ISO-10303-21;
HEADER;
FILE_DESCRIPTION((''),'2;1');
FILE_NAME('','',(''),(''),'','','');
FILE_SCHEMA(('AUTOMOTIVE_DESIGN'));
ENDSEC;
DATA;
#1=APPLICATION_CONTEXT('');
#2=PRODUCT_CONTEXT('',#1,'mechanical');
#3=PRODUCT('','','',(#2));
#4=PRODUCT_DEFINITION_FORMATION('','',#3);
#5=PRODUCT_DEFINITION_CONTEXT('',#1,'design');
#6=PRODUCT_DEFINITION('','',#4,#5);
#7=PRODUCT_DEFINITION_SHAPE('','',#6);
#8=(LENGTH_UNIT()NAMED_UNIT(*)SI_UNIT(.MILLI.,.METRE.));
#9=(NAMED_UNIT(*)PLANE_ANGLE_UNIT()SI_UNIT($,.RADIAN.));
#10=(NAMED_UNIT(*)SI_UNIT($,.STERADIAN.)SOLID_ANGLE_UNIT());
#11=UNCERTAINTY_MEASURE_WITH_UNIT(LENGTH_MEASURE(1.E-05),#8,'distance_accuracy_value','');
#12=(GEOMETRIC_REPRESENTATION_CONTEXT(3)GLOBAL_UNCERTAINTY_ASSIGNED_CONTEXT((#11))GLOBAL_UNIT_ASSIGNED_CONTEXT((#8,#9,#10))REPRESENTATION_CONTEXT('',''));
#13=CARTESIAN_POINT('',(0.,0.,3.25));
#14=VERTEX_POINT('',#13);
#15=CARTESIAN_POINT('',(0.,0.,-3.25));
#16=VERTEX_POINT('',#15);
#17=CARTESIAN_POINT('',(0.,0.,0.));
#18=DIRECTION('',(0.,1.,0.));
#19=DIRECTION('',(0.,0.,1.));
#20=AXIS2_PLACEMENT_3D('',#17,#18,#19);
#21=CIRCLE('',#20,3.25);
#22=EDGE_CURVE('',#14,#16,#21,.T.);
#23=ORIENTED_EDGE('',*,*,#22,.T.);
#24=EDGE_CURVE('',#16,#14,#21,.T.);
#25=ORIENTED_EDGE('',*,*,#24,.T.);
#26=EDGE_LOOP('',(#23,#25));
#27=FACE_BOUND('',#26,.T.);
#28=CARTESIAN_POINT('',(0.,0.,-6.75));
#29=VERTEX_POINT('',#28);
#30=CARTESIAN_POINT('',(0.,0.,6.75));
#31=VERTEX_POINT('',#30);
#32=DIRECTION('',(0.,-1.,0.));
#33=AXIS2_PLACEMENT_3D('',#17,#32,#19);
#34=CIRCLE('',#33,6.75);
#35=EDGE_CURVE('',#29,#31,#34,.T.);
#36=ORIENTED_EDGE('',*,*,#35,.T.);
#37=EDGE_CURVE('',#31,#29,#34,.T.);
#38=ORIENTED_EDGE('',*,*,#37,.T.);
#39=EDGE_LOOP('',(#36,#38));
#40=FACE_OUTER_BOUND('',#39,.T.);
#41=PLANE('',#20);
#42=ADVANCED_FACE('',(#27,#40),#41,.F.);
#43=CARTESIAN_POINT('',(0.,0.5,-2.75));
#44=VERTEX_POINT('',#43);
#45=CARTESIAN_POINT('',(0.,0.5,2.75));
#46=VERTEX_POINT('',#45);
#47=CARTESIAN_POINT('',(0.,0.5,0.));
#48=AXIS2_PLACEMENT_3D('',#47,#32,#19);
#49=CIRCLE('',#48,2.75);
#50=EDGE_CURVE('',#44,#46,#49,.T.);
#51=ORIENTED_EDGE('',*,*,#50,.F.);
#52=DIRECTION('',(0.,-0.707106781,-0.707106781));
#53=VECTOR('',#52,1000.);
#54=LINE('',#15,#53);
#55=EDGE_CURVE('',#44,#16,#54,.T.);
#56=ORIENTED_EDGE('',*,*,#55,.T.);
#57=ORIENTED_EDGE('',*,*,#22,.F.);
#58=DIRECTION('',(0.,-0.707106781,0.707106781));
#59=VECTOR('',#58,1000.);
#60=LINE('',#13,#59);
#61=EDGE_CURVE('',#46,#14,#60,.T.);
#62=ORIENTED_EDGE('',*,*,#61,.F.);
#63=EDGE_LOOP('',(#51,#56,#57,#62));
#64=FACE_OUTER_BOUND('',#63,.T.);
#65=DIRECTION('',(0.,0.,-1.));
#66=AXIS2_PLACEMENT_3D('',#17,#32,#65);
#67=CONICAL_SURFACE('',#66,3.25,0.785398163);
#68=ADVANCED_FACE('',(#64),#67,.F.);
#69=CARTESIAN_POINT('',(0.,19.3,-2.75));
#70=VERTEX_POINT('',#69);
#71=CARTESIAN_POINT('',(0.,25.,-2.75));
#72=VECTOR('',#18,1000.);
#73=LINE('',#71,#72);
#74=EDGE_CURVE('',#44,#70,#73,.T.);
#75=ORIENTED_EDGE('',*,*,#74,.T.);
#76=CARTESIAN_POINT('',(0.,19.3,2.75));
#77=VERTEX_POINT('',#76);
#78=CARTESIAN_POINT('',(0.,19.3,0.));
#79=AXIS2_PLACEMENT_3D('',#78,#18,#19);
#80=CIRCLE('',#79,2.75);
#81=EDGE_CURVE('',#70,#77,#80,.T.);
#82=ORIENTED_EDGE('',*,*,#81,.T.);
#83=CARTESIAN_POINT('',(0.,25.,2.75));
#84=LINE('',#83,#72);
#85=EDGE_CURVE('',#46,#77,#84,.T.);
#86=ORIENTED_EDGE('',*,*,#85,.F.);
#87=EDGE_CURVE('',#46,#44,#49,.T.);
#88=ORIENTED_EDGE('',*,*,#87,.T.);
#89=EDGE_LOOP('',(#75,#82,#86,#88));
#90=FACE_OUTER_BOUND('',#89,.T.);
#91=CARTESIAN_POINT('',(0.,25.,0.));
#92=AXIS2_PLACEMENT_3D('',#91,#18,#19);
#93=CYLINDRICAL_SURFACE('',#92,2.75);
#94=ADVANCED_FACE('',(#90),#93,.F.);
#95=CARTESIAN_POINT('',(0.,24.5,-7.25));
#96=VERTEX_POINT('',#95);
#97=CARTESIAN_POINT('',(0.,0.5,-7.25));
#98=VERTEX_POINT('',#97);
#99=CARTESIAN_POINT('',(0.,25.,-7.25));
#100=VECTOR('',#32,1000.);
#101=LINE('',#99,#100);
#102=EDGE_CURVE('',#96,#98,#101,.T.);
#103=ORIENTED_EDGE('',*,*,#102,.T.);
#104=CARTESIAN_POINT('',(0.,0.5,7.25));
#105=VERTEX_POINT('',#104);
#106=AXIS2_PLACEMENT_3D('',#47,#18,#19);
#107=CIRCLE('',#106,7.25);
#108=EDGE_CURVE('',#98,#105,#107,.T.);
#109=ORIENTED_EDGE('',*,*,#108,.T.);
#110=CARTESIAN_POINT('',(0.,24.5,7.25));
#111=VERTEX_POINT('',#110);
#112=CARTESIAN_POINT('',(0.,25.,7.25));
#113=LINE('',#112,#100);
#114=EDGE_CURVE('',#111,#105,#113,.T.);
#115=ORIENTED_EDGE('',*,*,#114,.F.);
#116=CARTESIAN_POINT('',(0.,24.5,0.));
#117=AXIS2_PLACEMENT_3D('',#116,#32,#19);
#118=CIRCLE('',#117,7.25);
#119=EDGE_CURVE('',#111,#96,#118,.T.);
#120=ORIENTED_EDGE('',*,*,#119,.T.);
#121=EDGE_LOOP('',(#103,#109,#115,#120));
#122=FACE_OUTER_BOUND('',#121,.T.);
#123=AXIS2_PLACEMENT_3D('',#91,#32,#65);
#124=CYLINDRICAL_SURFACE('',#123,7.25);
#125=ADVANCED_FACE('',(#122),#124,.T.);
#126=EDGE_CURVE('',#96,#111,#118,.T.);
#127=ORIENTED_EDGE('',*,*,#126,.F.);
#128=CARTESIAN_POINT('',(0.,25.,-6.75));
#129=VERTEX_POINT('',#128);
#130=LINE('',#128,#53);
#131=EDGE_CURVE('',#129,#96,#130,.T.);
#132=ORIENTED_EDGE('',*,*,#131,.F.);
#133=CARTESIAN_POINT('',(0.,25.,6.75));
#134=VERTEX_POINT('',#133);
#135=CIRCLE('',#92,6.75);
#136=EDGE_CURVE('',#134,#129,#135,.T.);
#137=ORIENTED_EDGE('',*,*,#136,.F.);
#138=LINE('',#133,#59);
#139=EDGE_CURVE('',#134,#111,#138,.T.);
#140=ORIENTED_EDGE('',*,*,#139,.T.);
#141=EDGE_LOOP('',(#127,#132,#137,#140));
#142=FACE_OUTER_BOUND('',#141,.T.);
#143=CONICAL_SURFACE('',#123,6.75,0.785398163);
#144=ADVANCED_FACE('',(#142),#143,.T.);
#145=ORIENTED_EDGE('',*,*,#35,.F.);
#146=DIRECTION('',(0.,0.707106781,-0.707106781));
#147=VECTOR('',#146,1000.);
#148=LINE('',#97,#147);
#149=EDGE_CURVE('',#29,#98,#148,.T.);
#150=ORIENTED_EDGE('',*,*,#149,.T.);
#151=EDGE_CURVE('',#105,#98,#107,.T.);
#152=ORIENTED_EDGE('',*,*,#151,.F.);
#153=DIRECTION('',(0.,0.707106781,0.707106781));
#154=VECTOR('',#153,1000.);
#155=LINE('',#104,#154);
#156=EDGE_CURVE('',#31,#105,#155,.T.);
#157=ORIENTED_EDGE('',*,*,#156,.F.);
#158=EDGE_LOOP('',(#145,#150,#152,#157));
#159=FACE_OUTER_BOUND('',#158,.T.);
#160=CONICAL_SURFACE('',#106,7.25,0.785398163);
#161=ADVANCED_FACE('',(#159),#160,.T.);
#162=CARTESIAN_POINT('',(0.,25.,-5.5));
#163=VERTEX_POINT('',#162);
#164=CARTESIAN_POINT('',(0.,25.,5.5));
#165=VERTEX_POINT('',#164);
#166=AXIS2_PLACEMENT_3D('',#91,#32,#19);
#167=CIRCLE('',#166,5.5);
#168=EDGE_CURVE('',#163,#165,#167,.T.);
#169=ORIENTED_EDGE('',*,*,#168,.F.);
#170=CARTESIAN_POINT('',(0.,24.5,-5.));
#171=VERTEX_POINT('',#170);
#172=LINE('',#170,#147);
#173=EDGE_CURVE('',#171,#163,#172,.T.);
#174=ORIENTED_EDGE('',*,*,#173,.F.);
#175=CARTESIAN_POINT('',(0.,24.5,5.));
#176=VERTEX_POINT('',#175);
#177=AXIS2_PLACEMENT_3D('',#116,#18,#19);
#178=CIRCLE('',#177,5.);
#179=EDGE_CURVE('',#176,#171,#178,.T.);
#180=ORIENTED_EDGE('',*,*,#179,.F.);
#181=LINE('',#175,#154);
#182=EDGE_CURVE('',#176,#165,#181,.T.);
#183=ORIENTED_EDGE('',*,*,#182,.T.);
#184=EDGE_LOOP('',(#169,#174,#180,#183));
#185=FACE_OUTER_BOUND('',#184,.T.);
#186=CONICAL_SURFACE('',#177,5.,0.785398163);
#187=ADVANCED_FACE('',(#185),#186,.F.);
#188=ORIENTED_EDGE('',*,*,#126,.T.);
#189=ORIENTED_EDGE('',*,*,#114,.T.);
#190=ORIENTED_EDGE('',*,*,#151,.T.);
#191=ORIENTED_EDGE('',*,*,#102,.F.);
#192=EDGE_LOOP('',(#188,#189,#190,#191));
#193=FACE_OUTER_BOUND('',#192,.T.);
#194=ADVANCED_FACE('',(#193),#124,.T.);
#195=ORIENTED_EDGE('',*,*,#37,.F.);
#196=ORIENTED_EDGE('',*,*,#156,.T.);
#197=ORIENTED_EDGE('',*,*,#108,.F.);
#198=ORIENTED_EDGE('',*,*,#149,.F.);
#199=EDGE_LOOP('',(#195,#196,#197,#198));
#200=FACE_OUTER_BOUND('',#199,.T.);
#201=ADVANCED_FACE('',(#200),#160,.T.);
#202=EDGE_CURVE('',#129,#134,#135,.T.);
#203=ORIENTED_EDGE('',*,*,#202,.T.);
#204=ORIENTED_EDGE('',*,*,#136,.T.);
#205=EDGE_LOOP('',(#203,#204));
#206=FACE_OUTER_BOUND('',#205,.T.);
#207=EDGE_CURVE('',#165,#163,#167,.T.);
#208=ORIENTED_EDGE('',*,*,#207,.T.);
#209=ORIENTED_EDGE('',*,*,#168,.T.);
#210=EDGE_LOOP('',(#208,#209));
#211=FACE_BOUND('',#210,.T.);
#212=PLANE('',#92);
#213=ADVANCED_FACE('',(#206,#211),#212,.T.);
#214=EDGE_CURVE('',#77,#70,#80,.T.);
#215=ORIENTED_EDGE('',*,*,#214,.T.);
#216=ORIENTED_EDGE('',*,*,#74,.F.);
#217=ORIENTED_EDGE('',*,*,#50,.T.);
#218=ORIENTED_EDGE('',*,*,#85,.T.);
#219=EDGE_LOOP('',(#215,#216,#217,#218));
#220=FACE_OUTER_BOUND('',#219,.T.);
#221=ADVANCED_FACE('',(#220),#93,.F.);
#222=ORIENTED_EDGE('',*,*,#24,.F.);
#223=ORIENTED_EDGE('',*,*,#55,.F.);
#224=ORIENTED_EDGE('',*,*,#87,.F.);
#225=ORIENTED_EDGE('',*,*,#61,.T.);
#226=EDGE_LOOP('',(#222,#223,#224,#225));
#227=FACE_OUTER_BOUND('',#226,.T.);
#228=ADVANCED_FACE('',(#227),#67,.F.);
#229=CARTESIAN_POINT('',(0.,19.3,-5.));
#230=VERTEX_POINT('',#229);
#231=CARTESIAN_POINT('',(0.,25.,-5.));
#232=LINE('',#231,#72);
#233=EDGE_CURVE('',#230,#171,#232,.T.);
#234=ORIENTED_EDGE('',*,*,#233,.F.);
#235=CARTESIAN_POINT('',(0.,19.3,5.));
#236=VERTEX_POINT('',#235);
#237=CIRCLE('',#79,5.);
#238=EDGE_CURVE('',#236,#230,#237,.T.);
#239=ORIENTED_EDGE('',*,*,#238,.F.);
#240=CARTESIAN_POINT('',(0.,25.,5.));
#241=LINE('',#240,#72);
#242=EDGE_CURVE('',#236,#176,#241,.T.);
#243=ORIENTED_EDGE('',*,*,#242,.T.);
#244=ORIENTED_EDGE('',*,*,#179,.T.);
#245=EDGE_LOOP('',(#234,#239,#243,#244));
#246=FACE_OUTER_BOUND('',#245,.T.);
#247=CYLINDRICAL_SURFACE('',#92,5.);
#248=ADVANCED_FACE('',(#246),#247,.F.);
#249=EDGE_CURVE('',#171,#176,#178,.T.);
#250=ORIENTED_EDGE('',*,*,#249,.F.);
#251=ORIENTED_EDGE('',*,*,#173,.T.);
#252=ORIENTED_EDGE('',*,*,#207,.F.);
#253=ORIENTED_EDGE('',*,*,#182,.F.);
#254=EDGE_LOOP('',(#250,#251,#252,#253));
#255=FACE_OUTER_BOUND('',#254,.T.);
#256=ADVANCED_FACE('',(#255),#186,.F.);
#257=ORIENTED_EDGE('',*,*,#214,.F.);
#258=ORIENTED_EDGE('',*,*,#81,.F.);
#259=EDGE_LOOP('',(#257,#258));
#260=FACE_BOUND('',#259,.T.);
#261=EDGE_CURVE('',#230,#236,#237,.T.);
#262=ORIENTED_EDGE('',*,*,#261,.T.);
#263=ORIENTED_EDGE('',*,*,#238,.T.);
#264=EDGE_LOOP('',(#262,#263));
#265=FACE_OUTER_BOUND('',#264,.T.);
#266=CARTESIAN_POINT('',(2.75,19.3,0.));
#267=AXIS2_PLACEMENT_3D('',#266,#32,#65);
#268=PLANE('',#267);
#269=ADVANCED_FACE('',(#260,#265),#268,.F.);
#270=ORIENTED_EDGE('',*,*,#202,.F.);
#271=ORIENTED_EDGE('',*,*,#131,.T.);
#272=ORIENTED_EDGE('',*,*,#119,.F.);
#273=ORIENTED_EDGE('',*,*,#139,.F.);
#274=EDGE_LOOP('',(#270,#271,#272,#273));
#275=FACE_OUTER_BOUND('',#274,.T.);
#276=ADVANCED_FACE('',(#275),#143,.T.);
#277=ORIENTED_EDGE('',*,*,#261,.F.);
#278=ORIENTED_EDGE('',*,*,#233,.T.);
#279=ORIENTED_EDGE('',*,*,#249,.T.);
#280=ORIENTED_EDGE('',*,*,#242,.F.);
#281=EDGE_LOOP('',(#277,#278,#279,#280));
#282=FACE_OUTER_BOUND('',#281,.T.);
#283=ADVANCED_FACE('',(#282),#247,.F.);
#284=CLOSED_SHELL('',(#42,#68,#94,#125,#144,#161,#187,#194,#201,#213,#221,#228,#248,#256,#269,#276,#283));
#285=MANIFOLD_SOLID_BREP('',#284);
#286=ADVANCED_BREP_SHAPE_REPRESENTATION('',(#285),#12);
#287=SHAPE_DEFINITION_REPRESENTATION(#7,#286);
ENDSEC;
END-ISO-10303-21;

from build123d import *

# Parameters (mm, degrees)
SKETCH1_R                                       = 7.25
BOSS_EXTRUDE1_DEPTH                             = 25
HOLE_SIZE_BY_HEX_SOCKET_SCREW_TYPE1_D           = 5.5
HOLE_SIZE_BY_HEX_SOCKET_SCREW_TYPE1_CBORE_D     = 10
HOLE_SIZE_BY_HEX_SOCKET_SCREW_TYPE1_CBORE_DEPTH = 5.7
CHAMFER1_SIZE                                   = 0.5


with BuildPart() as part:
    # Sketch1 → Boss-Extrude1 (new body)
    with BuildSketch(Plane(origin=(0, 0, 0), x_dir=(1, 0, 0), z_dir=(0, 1, 0))):
        with Locations(Location((0, 0, 0), (0, 0, 270))):
            Circle(SKETCH1_R)
    extrude(amount=BOSS_EXTRUDE1_DEPTH)

    # Hole Size by Hex Socket Screw Type1 (through all)
    with Locations(Plane(origin=(0, 25, 0), x_dir=(1, 0, 0), z_dir=(0, 1, 0))):
        with Locations((0, 0)):
            CounterBoreHole(HOLE_SIZE_BY_HEX_SOCKET_SCREW_TYPE1_D / 2, HOLE_SIZE_BY_HEX_SOCKET_SCREW_TYPE1_CBORE_D / 2, HOLE_SIZE_BY_HEX_SOCKET_SCREW_TYPE1_CBORE_DEPTH)

    # Chamfer1
    chamfer1_edges = [part.edges().sort_by_distance(p)[0] for p in [
        (0, 0, -7.25),
        (0, 25, -7.25),
        (-5, 25, 0),
        (2.75, 0, 0),
    ]]
    chamfer(chamfer1_edges, length=CHAMFER1_SIZE)


solid = part.part
